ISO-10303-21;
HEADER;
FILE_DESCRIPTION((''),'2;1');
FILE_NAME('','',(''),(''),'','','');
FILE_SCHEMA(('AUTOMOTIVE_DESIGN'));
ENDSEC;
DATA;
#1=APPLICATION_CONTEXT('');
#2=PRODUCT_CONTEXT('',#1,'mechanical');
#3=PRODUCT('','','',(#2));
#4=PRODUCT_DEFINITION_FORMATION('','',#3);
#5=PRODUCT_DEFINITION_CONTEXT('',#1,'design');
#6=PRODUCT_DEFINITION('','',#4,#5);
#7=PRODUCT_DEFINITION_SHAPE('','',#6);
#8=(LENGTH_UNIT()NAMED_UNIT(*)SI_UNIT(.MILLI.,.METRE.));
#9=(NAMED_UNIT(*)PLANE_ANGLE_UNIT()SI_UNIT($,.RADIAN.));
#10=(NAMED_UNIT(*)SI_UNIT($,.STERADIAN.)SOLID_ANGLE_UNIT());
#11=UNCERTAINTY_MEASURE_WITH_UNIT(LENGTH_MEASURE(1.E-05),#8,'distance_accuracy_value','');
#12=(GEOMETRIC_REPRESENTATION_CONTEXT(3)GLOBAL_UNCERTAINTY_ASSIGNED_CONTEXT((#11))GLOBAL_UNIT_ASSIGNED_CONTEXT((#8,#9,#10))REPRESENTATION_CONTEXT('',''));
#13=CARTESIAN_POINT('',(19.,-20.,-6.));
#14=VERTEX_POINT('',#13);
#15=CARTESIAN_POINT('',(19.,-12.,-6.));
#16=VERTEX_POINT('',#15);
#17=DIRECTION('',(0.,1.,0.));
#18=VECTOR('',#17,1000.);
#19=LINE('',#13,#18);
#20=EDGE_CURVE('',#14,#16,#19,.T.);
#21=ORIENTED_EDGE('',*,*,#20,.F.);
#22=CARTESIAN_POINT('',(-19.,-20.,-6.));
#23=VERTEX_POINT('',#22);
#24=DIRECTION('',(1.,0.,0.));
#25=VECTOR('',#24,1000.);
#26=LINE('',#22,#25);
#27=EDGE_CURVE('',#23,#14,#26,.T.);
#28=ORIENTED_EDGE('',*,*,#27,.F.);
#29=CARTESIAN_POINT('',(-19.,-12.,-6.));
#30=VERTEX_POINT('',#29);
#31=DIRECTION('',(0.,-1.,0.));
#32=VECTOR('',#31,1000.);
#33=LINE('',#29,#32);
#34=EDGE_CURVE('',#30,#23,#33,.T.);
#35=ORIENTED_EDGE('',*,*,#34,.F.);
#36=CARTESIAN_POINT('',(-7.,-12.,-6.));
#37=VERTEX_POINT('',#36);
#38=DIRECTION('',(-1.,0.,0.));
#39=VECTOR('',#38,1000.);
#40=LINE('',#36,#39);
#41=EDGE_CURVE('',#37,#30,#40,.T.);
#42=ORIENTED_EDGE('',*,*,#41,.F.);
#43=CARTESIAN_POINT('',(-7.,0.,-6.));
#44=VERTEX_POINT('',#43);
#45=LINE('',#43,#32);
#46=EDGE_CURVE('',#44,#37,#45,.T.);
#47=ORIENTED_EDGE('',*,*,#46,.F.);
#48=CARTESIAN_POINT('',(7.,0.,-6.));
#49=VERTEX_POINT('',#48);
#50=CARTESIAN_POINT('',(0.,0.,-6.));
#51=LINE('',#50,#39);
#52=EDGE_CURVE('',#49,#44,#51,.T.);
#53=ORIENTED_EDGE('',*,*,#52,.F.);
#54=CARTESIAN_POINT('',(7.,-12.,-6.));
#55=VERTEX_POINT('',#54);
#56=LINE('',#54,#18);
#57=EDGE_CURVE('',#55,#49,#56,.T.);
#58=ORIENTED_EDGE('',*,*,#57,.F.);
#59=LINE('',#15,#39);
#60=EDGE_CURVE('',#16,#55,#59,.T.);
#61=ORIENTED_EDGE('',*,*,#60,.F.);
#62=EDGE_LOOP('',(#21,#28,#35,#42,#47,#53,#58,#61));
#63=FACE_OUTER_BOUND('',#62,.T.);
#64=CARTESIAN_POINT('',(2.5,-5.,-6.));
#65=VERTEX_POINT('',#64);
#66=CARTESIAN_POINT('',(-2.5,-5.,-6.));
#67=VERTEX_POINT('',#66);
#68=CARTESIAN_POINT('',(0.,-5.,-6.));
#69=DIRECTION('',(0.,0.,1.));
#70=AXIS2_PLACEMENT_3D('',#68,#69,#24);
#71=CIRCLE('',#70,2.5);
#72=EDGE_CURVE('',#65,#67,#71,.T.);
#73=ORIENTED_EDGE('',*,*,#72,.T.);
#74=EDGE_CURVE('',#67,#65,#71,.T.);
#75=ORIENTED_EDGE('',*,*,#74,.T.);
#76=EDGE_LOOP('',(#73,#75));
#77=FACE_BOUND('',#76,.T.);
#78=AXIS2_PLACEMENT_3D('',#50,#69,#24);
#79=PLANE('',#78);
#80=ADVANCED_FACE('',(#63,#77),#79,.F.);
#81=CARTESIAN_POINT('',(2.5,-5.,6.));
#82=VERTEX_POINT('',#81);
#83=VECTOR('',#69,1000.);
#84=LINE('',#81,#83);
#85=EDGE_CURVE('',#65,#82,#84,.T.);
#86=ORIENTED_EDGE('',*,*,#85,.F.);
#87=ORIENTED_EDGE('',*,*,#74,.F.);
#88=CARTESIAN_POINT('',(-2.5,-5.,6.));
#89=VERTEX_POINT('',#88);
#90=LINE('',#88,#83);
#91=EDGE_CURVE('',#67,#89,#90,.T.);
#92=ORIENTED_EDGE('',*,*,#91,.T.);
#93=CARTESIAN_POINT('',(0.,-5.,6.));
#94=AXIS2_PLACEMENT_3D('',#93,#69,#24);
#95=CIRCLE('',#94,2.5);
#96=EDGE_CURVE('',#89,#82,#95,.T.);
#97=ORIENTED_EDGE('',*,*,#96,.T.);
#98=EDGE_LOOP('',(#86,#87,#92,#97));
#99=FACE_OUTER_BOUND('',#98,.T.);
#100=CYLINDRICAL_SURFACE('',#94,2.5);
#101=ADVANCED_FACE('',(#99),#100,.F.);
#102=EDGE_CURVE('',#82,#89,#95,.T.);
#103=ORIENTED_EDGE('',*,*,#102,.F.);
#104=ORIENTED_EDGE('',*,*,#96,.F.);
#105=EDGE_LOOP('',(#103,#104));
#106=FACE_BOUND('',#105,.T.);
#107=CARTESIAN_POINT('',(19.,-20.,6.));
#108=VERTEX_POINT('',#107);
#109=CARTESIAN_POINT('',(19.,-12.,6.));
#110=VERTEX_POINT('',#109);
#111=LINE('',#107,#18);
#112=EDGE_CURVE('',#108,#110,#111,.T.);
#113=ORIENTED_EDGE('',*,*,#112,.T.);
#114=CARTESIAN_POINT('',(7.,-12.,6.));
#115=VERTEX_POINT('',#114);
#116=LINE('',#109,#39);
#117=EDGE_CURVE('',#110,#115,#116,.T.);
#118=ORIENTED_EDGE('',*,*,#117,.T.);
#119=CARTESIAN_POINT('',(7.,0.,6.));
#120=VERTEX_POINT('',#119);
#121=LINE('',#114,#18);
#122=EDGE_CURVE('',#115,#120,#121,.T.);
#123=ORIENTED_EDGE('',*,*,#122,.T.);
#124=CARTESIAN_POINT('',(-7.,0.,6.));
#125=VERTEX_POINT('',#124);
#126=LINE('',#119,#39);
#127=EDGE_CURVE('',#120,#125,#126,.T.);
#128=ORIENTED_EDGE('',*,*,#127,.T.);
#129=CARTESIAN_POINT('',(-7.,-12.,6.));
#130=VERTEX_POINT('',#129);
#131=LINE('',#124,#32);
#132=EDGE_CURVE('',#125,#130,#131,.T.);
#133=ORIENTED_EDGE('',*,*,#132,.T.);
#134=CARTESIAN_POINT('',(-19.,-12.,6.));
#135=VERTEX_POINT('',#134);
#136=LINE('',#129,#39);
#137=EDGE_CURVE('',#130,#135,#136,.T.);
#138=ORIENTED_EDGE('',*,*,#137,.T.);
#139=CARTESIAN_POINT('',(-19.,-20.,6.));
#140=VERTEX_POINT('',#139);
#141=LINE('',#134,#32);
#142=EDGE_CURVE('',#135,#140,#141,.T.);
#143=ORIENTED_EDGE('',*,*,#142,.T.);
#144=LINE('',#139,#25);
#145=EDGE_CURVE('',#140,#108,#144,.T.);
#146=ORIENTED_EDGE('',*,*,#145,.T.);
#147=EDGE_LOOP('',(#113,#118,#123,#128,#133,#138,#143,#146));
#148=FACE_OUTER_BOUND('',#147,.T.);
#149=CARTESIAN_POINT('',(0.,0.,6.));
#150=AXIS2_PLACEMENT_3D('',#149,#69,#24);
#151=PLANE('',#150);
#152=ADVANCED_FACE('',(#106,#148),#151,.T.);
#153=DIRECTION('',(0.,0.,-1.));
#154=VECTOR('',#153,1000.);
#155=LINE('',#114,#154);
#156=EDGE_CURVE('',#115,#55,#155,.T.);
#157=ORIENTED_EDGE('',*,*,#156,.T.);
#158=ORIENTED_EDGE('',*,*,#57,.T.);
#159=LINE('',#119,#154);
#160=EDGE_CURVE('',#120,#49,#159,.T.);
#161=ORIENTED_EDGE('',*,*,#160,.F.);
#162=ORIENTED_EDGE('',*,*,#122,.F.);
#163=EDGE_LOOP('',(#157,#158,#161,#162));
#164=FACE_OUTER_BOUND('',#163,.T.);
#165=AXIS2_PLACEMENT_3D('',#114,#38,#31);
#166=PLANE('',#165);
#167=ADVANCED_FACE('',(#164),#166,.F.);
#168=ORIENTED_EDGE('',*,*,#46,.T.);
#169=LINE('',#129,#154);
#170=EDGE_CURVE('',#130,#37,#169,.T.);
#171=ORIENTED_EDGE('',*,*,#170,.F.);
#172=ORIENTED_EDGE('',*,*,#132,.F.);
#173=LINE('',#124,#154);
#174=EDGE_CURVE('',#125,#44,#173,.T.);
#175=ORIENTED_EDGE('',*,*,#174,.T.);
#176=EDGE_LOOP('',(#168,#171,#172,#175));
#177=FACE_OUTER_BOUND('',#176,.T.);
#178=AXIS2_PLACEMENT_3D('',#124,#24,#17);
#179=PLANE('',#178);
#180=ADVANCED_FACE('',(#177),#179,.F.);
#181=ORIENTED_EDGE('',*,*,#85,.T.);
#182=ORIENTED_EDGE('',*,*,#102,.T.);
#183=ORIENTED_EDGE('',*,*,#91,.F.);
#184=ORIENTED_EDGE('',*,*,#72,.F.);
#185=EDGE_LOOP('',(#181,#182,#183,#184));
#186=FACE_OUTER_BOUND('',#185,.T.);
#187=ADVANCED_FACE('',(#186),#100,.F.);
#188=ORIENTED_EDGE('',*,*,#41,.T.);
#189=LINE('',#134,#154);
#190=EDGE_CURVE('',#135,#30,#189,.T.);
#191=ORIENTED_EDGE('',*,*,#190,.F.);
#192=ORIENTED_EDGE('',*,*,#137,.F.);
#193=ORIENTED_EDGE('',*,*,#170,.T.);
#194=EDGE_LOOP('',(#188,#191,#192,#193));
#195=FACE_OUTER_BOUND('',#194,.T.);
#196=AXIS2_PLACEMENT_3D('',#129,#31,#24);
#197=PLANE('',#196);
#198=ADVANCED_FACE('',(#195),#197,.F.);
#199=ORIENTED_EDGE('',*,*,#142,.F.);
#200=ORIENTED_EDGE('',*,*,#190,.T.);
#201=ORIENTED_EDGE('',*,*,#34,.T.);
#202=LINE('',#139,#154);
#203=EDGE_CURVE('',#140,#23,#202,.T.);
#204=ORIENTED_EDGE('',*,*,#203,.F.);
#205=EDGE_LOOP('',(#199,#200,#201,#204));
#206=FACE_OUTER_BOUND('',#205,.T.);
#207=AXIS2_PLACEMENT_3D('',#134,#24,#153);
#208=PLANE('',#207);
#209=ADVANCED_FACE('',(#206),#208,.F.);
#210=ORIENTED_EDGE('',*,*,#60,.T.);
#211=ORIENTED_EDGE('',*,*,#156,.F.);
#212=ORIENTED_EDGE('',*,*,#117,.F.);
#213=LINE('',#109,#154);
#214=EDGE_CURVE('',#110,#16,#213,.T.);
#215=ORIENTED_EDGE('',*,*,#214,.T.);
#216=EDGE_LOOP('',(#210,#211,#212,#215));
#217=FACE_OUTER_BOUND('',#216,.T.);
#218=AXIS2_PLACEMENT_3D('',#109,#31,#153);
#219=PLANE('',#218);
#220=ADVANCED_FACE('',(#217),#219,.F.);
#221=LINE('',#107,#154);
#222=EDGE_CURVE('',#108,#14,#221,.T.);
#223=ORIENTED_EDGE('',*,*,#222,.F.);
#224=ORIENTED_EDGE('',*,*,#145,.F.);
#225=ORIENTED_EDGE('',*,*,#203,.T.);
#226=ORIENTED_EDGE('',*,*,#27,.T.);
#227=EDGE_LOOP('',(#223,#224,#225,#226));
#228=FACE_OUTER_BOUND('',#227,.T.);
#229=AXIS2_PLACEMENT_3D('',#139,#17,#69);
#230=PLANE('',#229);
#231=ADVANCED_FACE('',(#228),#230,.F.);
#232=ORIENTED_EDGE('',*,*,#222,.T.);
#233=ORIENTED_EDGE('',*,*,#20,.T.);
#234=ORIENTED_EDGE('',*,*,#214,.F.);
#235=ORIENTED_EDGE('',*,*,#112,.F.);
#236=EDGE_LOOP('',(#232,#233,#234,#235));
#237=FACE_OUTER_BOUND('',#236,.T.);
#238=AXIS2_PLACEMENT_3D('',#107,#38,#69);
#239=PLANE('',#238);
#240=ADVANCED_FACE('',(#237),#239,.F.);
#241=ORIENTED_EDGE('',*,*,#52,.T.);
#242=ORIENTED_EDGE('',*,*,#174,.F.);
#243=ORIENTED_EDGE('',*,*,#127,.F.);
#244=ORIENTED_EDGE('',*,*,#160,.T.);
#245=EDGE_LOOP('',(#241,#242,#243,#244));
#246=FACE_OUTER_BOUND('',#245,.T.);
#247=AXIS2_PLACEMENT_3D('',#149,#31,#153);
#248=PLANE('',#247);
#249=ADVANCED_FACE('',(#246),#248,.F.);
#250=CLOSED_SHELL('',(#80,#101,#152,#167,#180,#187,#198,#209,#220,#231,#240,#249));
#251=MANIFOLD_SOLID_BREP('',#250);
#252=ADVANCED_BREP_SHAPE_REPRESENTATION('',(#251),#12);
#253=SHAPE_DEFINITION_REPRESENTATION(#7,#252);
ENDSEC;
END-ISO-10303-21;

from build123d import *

# Parameters (mm, degrees)
EXTRUDE_1_DEPTH    = 6
HOLE_WIZARD_M6_1_D = 5


with BuildPart() as part:
    # 草图1 → 凸台-拉伸1 (new, symmetric)
    with BuildSketch(Plane.XY):
        Polygon((0, 0), (-7, 0), (-7, -12), (-19, -12), (-19, -20), (19, -20), (19, -12), (7, -12), (7, 0), align=None)
    extrude(amount=EXTRUDE_1_DEPTH, both=True)

    # M6 螺纹孔1 (through all)
    with Locations(Plane(origin=(0, -5, 6), x_dir=(1, 0, 0), z_dir=(0, 0, 1))):
        with Locations((0, 0)):
            Hole(HOLE_WIZARD_M6_1_D / 2)


solid = part.part
